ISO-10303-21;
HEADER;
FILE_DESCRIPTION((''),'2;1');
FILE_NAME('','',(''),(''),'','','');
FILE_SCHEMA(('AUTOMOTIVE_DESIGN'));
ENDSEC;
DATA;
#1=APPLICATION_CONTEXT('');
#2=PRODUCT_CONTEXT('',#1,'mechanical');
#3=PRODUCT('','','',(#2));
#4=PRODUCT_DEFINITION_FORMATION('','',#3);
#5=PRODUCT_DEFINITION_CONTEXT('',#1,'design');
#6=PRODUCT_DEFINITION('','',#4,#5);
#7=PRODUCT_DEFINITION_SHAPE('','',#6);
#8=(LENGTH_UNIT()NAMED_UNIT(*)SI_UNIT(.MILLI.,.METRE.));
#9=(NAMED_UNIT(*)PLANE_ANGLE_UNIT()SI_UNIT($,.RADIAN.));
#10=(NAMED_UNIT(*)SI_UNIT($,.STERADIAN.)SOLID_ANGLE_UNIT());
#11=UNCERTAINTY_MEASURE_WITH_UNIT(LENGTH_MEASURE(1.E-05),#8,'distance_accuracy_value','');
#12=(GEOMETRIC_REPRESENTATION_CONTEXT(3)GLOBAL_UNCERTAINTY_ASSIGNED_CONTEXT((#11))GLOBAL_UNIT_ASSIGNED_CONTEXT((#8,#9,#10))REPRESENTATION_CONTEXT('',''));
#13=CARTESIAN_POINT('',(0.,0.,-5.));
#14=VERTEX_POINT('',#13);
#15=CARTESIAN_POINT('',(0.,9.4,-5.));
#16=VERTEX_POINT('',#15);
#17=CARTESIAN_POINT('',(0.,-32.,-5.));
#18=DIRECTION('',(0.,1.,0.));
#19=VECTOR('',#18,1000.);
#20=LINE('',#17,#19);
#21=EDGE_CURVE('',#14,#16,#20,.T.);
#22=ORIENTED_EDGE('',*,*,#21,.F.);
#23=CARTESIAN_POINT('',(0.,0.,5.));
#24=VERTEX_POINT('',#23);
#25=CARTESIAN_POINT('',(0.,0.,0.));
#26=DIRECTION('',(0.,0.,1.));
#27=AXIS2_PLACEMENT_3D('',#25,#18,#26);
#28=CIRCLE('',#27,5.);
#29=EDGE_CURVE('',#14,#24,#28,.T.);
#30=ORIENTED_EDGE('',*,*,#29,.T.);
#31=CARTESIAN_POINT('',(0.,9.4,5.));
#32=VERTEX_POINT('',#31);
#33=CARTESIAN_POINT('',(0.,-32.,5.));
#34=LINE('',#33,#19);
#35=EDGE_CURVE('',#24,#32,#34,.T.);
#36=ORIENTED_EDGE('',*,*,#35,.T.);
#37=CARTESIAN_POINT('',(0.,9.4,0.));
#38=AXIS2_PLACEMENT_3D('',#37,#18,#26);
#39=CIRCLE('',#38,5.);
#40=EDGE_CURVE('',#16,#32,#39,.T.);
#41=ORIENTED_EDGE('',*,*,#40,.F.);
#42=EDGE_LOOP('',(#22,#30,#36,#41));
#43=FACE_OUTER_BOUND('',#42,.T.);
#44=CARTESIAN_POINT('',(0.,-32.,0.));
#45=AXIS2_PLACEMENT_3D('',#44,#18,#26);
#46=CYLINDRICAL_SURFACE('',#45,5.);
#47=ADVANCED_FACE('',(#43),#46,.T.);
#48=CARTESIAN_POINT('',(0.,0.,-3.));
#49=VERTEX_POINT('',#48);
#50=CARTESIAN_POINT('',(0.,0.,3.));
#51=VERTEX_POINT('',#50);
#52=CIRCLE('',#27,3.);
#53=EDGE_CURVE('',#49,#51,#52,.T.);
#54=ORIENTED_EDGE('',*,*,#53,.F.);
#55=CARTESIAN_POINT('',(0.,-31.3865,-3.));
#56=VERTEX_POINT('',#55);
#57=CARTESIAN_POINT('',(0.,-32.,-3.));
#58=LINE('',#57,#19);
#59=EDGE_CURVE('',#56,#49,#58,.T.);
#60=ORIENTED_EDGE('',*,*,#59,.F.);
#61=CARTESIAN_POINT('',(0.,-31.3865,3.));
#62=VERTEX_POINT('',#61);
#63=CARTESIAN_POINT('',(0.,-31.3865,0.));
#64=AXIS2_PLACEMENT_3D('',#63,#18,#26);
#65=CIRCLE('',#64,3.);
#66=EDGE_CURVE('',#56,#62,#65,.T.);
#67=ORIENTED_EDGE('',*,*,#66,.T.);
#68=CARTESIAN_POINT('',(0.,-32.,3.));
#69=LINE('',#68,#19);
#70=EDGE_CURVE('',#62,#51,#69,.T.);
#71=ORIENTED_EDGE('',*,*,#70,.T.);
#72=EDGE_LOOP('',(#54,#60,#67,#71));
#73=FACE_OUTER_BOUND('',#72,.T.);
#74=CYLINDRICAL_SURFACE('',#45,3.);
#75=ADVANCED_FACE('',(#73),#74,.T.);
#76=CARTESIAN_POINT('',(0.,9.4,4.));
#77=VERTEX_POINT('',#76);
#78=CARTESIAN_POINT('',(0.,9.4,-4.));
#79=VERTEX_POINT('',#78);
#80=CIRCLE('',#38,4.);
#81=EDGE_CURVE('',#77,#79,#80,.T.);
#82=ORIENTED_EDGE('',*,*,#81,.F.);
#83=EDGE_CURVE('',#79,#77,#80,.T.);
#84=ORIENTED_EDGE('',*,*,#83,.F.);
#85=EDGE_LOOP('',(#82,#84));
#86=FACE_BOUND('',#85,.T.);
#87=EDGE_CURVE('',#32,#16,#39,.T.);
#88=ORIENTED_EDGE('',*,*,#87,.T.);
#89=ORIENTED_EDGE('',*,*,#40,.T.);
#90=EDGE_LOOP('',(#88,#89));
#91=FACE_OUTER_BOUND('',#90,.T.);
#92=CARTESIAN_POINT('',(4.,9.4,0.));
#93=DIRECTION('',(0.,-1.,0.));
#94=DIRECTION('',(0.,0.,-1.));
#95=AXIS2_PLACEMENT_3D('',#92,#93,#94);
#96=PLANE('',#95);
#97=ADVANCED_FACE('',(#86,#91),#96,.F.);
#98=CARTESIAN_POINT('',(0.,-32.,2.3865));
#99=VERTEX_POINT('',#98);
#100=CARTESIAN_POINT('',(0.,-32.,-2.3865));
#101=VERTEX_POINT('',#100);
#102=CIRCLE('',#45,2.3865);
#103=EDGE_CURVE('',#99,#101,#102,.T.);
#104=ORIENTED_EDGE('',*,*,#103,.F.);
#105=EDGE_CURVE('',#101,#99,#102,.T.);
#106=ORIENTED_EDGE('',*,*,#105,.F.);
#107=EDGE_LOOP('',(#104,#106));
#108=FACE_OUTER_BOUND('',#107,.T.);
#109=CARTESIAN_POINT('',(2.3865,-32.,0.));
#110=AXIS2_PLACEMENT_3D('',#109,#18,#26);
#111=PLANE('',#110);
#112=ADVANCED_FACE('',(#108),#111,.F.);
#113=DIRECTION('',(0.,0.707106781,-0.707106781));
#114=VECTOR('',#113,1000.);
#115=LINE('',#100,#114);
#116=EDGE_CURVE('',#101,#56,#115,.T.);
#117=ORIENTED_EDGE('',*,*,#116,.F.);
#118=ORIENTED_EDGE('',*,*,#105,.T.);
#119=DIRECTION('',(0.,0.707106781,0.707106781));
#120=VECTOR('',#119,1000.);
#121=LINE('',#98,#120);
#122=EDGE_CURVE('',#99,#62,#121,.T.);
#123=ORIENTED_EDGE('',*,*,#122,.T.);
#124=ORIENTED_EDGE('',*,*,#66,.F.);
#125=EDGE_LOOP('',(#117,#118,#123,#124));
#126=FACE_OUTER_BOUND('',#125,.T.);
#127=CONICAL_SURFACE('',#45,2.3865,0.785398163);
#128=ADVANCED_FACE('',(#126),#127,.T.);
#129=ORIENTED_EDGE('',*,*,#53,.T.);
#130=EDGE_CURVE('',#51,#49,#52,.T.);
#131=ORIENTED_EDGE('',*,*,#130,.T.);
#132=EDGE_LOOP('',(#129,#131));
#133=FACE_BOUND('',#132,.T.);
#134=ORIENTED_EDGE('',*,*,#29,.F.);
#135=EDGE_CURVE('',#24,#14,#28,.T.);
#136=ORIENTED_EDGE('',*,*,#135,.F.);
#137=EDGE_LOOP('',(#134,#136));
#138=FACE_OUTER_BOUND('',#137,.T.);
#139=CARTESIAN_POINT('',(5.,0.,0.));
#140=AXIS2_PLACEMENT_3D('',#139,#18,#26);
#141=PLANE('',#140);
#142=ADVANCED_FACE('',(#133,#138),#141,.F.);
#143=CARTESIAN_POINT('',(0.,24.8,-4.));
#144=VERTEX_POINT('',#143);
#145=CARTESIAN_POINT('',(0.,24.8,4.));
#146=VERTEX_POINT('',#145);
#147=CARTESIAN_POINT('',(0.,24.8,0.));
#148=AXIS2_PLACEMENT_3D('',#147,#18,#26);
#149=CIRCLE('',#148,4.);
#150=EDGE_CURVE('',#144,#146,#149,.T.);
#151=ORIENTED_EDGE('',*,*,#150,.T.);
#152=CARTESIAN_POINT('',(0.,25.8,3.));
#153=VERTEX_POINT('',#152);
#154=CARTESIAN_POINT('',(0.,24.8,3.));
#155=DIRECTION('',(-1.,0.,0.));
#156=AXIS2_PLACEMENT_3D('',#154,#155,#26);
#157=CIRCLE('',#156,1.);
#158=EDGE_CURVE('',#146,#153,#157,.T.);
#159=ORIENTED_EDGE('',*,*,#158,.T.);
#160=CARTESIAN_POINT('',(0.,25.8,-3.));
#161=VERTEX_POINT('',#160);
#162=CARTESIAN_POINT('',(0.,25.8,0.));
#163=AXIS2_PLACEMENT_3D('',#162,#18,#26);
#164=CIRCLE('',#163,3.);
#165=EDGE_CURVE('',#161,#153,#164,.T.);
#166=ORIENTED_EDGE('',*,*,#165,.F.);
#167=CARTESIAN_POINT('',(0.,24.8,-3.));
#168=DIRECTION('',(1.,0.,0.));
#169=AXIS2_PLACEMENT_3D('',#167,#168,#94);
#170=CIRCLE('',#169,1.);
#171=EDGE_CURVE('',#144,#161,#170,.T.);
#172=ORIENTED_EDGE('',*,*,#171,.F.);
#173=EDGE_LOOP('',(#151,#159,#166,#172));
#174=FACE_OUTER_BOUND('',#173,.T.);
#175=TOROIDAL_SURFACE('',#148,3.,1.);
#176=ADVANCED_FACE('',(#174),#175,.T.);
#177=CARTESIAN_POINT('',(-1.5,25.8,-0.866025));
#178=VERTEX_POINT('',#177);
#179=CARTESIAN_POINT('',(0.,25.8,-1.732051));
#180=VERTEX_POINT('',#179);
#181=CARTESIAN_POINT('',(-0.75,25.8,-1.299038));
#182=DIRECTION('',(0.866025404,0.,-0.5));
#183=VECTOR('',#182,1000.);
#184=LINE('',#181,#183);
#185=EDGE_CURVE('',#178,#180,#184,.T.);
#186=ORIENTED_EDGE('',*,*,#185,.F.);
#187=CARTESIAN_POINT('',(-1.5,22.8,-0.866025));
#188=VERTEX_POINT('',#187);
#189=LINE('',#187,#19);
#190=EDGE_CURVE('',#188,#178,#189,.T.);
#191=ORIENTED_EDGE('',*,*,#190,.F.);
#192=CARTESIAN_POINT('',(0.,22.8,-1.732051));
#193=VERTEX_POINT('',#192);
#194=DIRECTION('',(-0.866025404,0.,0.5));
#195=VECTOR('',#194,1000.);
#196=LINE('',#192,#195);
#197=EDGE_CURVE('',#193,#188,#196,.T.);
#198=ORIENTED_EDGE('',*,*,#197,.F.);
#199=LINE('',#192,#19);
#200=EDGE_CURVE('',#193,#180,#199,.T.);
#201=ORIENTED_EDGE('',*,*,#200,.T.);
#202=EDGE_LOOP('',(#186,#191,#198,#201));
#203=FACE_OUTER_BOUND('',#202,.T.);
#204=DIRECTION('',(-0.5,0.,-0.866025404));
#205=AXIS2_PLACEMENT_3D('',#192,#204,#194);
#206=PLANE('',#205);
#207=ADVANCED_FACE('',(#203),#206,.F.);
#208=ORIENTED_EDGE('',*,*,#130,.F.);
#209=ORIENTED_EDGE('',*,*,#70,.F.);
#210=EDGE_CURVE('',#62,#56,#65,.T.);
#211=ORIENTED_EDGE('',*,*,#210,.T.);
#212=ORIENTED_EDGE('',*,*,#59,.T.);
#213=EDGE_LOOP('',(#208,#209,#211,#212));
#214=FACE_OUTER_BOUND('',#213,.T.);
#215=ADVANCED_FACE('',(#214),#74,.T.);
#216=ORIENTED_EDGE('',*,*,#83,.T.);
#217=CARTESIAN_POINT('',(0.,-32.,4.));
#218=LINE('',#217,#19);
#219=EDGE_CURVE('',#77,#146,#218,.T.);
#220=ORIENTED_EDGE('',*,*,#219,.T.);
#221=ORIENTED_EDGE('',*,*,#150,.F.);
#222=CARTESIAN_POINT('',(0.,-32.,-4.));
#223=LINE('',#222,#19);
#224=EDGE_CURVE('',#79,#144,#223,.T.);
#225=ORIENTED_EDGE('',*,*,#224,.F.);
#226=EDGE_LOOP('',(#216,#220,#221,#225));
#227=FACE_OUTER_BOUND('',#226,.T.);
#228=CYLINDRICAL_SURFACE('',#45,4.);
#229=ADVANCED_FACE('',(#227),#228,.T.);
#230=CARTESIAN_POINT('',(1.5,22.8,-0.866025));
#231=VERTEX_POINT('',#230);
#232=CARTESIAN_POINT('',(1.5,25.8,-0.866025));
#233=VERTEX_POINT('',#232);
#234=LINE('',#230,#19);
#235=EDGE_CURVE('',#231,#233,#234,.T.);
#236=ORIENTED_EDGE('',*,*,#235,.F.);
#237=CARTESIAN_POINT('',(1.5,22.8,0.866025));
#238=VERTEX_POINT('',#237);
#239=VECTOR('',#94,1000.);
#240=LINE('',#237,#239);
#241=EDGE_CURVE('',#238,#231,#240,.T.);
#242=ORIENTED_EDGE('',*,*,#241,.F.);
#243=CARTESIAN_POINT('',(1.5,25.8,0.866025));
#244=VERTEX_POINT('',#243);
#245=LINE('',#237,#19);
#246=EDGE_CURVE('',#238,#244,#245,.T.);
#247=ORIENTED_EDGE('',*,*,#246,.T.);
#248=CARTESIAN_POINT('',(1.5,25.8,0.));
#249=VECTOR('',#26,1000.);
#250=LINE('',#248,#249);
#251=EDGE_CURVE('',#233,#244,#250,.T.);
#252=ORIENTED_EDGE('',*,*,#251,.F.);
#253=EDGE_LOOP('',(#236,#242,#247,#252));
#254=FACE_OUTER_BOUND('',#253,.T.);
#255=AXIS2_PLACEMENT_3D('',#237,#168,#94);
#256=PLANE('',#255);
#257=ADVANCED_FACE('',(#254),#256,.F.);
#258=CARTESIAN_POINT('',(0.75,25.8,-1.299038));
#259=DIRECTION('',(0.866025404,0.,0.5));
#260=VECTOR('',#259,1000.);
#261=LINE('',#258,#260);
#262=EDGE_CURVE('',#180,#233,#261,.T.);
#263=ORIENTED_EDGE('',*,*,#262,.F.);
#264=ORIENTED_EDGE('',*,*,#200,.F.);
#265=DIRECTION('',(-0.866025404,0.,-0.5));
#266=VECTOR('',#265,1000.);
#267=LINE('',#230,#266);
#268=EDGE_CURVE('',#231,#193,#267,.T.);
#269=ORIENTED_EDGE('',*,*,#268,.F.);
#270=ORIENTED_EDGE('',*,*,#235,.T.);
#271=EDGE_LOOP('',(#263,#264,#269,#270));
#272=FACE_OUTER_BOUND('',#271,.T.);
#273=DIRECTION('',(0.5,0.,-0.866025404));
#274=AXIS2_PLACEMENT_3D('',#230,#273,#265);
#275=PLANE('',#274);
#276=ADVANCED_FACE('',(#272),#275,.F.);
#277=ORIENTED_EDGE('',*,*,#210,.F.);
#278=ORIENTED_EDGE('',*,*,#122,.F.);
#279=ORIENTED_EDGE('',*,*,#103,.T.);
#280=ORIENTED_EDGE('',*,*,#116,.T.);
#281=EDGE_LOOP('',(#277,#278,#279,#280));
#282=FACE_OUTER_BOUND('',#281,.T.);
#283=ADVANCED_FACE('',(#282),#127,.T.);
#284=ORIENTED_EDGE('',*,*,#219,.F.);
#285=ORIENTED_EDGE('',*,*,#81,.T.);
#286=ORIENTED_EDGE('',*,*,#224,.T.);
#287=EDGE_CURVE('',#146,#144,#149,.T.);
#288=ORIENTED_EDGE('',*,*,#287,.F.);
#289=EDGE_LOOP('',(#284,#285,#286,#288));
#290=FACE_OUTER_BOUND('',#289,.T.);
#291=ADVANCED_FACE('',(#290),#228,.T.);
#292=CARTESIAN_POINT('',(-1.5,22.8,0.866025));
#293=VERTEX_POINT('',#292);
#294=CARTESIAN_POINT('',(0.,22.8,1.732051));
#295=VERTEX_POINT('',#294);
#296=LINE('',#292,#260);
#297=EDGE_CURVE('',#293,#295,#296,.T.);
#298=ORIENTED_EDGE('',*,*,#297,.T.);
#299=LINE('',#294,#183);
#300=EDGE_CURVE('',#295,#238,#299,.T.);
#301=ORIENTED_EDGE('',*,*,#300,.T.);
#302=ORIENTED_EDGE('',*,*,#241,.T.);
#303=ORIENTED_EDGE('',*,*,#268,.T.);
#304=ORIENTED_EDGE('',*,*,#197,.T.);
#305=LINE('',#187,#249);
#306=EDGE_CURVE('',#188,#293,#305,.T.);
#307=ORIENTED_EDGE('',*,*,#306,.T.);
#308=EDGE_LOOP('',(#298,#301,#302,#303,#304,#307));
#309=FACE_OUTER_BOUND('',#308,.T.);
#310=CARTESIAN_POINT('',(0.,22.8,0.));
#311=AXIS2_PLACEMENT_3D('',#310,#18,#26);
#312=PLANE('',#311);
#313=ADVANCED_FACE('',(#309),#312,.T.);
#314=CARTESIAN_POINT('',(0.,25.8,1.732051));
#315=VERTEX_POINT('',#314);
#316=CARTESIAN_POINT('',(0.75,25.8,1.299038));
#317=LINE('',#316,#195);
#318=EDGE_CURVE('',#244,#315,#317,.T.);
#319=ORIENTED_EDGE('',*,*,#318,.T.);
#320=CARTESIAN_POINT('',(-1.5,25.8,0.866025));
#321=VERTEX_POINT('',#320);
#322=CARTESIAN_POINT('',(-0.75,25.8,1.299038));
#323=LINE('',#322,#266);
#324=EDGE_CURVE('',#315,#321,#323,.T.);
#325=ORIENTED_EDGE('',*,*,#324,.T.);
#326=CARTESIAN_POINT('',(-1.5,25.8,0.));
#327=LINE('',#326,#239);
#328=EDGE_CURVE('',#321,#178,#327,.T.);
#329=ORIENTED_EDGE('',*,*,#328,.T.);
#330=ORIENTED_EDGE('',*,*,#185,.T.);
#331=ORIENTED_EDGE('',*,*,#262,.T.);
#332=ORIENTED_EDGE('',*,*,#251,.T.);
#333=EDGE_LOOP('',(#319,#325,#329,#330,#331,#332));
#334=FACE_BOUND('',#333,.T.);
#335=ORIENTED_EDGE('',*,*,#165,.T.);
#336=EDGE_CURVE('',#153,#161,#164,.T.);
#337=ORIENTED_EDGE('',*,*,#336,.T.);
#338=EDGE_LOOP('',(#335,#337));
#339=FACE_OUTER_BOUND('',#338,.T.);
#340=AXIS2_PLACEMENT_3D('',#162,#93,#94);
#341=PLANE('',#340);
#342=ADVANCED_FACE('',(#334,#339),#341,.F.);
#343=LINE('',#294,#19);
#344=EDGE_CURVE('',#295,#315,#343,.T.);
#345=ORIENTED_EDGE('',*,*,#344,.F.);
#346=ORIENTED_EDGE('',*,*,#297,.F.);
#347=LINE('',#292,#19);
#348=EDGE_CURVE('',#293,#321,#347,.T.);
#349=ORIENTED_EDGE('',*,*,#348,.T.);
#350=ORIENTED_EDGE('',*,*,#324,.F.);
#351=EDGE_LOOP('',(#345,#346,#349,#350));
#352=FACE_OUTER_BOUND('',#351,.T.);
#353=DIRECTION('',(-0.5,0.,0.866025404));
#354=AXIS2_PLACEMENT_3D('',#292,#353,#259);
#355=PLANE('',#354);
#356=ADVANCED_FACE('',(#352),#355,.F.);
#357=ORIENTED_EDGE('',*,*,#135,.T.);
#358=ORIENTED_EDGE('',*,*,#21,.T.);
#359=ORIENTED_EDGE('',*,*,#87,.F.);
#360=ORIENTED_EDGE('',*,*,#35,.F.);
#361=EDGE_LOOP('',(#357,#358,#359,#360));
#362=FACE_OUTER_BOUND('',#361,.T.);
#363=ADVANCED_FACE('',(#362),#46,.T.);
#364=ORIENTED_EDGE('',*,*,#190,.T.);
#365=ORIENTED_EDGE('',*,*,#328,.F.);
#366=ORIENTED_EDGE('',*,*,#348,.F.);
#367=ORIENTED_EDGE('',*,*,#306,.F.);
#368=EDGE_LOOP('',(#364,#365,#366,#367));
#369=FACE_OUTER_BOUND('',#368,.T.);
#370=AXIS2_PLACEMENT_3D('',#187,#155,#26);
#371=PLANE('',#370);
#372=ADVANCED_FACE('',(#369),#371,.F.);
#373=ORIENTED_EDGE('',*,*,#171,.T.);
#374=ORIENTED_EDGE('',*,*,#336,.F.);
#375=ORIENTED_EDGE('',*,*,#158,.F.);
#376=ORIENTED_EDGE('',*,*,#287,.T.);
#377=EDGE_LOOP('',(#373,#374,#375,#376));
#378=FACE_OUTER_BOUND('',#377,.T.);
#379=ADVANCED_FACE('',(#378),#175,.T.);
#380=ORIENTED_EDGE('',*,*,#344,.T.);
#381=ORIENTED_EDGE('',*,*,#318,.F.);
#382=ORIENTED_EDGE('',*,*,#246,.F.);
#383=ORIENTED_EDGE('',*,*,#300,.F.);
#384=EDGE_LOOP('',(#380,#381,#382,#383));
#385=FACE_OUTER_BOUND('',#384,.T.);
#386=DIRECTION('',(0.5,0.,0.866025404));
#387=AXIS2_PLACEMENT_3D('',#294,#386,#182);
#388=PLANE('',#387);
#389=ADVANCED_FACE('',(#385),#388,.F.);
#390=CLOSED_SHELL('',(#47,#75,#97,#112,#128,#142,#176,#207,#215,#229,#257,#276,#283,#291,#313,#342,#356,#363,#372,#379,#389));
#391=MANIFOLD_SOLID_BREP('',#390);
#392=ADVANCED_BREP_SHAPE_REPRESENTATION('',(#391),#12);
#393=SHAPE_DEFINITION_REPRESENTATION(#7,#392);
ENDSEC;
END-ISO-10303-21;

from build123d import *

# Parameters (mm, degrees)
CUT_EXTRUDE_1_DEPTH      = 3
CUT_EXTRUDE_1_DEPTH_BACK = 3


with BuildPart() as part:
    # 草图1 → 旋转1 (revolve)
    with BuildSketch(Plane.XY, mode=Mode.PRIVATE) as revolve_1_sk:
        with BuildLine():
            Line((0, 25.8), (3, 25.8))
            ThreePointArc((3, 25.8), (3.707106781, 25.507106781), (4, 24.8))
            Line((4, 24.8), (4, 9.4))
            Line((4, 9.4), (5, 9.4))
            Line((5, 9.4), (5, 0))
            Line((5, 0), (3, 0))
            Line((3, 0), (3, -31.3865))
            Line((3, -31.3865), (2.3865, -32))
            Line((2.3865, -32), (0, -32))
            Line((0, -32), (0, 25.8))
        make_face()
    revolve(revolve_1_sk.sketch.rotate(Axis((0, -32, 0), (0, 1, 0)), 270), axis=Axis((0, -32, 0), (0, 1, 0)))

    # 草图2 → 切除-拉伸1 (cut, two sides: drawn at the far end of the back side and taken through both)
    with BuildSketch(Plane(origin=(0, 25.8, 0), x_dir=(1, 0, 0), z_dir=(0, 1, 0)).offset(-CUT_EXTRUDE_1_DEPTH_BACK)):
        Polygon((-1.5, 0.866025404), (-1.5, -0.866025404), (0, -1.732050808), (1.5, -0.866025404), (1.5, 0.866025404), (0, 1.732050808), align=None)
    extrude(amount=CUT_EXTRUDE_1_DEPTH + CUT_EXTRUDE_1_DEPTH_BACK, mode=Mode.SUBTRACT)


solid = part.part
